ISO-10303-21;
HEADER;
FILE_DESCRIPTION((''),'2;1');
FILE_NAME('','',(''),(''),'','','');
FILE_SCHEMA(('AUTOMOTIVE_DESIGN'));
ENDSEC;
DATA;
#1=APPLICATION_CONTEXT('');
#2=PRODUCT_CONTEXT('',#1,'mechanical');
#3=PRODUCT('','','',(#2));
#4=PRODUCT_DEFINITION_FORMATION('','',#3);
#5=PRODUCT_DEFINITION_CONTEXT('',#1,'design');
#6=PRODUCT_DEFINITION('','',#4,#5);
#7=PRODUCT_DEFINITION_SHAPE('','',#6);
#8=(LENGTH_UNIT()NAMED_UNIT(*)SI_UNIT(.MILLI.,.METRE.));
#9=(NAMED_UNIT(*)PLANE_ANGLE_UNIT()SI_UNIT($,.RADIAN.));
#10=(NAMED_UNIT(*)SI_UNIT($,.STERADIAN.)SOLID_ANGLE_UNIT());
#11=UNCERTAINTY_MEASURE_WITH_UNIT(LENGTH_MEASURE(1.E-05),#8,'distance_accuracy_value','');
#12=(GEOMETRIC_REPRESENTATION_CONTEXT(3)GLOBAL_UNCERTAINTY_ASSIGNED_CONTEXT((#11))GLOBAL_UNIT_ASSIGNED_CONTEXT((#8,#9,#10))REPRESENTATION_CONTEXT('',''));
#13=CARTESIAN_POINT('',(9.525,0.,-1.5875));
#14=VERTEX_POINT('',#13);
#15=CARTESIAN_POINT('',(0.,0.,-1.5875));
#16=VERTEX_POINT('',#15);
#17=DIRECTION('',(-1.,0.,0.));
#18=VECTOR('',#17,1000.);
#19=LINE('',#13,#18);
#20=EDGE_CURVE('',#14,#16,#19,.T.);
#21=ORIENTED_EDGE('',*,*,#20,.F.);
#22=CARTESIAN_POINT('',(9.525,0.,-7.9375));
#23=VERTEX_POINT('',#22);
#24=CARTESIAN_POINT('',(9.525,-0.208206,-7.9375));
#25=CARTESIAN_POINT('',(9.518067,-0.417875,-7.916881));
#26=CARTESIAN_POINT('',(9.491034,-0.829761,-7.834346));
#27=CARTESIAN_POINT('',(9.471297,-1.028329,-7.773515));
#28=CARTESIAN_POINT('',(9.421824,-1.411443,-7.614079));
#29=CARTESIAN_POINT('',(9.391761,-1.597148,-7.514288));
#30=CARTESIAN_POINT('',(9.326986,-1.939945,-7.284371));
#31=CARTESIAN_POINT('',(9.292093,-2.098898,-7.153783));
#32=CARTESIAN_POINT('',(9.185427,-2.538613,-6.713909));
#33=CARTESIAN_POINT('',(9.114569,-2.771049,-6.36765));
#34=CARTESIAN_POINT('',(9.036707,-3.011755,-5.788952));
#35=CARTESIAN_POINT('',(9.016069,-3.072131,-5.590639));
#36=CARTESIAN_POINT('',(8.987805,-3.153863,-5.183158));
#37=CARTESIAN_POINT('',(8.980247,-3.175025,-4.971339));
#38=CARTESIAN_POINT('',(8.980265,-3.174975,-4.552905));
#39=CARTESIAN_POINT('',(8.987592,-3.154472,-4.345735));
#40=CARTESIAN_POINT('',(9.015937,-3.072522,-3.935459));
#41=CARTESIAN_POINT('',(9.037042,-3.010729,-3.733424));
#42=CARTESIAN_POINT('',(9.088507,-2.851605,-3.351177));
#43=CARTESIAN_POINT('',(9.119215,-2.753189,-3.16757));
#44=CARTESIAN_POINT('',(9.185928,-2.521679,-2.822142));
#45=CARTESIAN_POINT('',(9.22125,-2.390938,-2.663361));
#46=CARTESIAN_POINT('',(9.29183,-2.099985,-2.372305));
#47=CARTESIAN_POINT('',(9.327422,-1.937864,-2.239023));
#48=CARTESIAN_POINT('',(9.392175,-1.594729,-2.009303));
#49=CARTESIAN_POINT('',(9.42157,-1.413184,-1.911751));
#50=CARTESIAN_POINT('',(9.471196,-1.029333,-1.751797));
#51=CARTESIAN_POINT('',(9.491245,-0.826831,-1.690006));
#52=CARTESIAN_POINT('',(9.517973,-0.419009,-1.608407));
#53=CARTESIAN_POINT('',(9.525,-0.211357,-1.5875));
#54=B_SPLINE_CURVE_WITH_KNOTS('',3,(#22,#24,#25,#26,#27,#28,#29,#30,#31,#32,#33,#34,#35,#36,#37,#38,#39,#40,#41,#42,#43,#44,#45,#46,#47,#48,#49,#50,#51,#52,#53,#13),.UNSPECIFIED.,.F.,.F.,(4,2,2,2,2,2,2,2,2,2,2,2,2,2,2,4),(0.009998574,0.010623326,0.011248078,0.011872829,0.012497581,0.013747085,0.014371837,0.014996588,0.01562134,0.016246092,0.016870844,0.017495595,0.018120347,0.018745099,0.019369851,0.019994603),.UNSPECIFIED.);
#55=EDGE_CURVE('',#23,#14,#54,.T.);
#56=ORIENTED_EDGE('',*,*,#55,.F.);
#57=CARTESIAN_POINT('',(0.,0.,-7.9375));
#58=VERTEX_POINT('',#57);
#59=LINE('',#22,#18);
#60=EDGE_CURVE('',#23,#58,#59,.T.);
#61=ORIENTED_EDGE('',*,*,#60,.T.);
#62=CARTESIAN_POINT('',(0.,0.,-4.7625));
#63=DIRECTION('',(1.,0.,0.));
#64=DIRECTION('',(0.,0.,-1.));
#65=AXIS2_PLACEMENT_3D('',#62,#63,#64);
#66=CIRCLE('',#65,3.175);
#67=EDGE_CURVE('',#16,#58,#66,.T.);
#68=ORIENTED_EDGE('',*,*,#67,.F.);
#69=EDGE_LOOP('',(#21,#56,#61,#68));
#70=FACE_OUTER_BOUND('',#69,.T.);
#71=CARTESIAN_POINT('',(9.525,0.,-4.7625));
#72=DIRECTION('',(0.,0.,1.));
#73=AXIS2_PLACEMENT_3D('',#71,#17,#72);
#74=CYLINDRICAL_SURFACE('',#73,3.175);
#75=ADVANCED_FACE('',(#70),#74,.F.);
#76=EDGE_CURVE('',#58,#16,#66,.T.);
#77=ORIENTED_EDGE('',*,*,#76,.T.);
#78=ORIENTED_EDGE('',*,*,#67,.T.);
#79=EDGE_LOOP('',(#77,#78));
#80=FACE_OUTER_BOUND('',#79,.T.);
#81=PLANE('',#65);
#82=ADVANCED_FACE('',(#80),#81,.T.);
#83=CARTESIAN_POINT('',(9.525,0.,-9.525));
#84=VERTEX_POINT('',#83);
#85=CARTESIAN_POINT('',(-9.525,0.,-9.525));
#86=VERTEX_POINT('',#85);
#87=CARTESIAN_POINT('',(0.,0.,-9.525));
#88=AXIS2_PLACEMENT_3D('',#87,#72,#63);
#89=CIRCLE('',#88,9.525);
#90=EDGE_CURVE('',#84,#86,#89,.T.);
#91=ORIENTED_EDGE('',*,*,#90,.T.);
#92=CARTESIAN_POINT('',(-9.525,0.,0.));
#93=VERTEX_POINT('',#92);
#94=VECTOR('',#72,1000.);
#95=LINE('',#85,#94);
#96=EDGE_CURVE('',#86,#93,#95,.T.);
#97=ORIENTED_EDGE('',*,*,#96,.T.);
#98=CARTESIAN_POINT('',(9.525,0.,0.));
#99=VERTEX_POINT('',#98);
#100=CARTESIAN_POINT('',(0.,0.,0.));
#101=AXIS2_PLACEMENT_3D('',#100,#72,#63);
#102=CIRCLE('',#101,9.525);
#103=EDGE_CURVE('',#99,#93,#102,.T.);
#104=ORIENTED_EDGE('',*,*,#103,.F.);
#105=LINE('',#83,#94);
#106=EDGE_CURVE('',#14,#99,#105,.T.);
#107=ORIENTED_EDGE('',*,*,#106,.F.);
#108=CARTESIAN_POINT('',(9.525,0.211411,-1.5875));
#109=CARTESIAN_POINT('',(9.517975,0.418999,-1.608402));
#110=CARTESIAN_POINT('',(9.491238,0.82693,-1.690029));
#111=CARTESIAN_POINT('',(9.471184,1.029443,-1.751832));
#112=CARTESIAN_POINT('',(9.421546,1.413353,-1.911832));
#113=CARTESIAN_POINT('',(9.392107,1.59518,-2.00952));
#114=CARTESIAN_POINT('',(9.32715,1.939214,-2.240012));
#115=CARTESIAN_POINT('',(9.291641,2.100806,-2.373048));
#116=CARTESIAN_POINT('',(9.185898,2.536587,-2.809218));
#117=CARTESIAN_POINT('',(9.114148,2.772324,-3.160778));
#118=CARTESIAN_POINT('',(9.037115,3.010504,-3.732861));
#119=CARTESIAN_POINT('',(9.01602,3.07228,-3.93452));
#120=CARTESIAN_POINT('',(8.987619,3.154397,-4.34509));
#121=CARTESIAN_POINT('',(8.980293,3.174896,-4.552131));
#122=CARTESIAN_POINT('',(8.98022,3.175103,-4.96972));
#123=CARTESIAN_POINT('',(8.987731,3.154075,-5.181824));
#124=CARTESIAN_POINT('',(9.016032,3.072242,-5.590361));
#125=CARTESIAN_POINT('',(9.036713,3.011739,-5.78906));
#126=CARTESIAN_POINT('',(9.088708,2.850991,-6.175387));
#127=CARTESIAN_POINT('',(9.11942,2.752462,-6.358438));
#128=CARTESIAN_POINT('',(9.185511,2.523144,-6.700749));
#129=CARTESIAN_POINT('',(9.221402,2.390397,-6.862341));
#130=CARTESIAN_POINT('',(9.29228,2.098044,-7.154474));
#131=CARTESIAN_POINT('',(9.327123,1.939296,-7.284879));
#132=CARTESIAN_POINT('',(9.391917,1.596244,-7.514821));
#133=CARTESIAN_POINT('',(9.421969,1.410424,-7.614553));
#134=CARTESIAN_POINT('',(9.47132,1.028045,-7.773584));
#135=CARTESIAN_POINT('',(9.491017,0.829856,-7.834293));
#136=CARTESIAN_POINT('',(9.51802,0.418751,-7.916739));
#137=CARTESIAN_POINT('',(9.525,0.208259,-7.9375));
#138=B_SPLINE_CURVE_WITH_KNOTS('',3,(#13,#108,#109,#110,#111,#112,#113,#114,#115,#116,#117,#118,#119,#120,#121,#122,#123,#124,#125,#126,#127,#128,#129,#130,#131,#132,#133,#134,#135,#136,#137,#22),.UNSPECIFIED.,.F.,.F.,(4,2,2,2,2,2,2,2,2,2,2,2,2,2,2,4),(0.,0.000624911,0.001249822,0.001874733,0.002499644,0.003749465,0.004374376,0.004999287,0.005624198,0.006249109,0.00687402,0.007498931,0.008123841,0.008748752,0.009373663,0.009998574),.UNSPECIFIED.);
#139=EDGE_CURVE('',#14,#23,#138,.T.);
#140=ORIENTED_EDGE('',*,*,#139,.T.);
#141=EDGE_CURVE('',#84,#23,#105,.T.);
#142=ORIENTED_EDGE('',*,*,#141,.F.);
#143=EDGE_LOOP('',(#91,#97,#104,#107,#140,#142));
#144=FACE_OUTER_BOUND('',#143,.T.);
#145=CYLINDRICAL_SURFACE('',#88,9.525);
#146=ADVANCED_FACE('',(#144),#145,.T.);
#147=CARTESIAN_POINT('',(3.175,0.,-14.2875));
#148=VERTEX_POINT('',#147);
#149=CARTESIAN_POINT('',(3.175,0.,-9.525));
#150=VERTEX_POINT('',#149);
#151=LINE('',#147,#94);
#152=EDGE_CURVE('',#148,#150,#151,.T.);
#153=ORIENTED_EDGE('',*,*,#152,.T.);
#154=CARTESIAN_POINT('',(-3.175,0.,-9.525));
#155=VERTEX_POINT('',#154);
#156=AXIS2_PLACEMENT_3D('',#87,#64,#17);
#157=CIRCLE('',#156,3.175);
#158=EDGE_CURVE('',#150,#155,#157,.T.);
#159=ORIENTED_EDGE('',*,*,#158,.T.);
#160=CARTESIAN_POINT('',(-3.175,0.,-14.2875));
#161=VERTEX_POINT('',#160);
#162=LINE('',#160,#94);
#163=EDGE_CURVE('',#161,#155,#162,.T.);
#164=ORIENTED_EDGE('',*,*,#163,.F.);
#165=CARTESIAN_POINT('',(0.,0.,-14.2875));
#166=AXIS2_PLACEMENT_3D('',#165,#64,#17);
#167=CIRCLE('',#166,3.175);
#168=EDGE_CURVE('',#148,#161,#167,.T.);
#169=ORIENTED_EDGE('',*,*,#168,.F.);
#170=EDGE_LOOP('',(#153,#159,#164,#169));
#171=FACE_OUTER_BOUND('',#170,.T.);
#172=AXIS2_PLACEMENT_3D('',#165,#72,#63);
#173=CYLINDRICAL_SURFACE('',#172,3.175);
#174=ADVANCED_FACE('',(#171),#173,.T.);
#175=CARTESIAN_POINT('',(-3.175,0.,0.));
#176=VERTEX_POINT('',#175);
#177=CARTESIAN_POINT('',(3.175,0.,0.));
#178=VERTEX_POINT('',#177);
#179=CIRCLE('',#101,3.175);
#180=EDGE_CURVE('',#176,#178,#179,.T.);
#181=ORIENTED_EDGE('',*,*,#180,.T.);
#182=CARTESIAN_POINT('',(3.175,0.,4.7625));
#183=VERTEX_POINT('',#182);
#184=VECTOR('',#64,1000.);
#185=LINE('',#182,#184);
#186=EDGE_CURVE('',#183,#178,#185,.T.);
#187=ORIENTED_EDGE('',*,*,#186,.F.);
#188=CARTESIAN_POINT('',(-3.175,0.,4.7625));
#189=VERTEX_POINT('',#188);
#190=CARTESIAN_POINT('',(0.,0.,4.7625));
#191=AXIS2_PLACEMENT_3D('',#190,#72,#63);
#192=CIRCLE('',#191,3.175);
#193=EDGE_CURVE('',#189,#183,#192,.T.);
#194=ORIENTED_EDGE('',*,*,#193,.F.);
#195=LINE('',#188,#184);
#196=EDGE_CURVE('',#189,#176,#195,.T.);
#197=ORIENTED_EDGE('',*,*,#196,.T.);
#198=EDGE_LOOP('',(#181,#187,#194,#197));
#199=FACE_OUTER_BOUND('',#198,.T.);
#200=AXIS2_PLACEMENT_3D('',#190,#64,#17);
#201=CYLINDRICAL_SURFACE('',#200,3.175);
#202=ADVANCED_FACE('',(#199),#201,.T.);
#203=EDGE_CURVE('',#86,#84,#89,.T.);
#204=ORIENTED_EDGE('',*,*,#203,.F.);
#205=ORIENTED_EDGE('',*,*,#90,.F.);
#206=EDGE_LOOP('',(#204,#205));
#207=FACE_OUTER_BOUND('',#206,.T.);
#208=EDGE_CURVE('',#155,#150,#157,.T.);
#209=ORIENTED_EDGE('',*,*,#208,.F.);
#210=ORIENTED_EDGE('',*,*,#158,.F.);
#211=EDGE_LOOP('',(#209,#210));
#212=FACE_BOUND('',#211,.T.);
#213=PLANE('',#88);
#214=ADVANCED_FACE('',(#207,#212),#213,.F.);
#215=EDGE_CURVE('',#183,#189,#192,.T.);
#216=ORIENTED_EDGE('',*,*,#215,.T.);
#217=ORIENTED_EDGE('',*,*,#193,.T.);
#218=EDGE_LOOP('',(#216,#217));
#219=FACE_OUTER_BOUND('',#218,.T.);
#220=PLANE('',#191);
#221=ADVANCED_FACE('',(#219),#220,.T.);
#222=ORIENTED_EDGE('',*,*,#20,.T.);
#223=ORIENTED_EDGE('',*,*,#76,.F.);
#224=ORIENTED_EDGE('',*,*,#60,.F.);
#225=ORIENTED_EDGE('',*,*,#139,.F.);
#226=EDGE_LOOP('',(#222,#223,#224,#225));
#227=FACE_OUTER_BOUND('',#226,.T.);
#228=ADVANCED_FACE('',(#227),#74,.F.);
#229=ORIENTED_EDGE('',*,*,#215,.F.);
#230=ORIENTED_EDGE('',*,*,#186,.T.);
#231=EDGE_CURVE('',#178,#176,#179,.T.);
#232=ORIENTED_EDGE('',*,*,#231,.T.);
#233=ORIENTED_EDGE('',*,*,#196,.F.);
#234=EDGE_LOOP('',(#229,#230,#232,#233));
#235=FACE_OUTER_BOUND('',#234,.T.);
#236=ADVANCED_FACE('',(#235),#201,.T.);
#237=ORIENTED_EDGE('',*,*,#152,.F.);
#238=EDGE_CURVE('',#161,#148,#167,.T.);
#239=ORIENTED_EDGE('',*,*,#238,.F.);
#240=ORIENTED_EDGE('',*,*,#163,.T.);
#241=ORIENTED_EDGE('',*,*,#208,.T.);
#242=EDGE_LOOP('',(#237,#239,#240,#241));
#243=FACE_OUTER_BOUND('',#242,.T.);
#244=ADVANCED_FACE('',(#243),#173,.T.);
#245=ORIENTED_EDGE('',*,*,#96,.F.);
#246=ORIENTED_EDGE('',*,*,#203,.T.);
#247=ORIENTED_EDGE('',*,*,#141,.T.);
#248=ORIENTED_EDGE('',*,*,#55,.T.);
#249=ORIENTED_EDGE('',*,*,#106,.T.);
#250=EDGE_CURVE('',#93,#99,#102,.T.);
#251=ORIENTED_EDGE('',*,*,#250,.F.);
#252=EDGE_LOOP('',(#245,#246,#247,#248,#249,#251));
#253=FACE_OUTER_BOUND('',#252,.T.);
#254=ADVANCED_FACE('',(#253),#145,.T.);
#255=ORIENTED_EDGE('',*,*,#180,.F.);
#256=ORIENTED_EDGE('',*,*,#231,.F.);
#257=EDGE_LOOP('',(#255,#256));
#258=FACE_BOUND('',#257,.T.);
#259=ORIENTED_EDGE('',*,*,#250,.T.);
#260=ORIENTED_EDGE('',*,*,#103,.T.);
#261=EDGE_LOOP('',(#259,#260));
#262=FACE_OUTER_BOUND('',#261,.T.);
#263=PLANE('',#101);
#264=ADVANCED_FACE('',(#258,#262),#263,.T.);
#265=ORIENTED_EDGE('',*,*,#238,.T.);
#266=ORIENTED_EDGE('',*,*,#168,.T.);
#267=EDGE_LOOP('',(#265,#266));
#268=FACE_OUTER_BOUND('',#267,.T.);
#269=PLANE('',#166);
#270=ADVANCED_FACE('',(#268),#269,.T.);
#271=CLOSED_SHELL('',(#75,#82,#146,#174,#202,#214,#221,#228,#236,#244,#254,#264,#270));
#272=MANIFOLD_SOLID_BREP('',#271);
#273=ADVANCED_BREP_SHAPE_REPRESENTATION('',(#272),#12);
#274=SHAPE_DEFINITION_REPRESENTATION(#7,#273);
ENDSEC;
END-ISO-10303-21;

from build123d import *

# Parameters (mm, degrees)
SKETCH1_R           = 9.525
BOSS_EXTRUDE1_DEPTH = 9.525
SKETCH2_R           = 3.175
BOSS_EXTRUDE2_DEPTH = 4.7625
BOSS_EXTRUDE3_START = 4.7625
SKETCH3_R           = 3.175
BOSS_EXTRUDE3_DEPTH = 4.7625
SKETCH4_R           = 3.175
CUT_EXTRUDE1_DEPTH  = 20.636290542


with BuildPart() as part:
    # Sketch1 → Boss-Extrude1 (new body)
    with BuildSketch(Plane.XY):
        Circle(SKETCH1_R)
    extrude(amount=-BOSS_EXTRUDE1_DEPTH)

    # Sketch2 → Boss-Extrude2 (add)
    with BuildSketch(Plane.XY):
        with Locations(Location((0, 0, 0), (0, 0, 180))):
            Circle(SKETCH2_R)
    extrude(amount=BOSS_EXTRUDE2_DEPTH)

    # Sketch3 → Boss-Extrude3 (add)
    with BuildSketch(Plane(origin=(0, 0, -9.525), x_dir=(-1, 0, 0), z_dir=(0, 0, -1)).offset(BOSS_EXTRUDE3_START)):
        Circle(SKETCH3_R)
    extrude(amount=-BOSS_EXTRUDE3_DEPTH)

    # Sketch4 → Cut-Extrude1 (cut, through all)
    with BuildSketch(Plane(origin=(0, 0, 0), x_dir=(0, 0, -1), z_dir=(1, 0, 0))):
        with Locations((4.7625, 0)):
            Circle(SKETCH4_R)
    extrude(amount=CUT_EXTRUDE1_DEPTH, mode=Mode.SUBTRACT)


solid = part.part
